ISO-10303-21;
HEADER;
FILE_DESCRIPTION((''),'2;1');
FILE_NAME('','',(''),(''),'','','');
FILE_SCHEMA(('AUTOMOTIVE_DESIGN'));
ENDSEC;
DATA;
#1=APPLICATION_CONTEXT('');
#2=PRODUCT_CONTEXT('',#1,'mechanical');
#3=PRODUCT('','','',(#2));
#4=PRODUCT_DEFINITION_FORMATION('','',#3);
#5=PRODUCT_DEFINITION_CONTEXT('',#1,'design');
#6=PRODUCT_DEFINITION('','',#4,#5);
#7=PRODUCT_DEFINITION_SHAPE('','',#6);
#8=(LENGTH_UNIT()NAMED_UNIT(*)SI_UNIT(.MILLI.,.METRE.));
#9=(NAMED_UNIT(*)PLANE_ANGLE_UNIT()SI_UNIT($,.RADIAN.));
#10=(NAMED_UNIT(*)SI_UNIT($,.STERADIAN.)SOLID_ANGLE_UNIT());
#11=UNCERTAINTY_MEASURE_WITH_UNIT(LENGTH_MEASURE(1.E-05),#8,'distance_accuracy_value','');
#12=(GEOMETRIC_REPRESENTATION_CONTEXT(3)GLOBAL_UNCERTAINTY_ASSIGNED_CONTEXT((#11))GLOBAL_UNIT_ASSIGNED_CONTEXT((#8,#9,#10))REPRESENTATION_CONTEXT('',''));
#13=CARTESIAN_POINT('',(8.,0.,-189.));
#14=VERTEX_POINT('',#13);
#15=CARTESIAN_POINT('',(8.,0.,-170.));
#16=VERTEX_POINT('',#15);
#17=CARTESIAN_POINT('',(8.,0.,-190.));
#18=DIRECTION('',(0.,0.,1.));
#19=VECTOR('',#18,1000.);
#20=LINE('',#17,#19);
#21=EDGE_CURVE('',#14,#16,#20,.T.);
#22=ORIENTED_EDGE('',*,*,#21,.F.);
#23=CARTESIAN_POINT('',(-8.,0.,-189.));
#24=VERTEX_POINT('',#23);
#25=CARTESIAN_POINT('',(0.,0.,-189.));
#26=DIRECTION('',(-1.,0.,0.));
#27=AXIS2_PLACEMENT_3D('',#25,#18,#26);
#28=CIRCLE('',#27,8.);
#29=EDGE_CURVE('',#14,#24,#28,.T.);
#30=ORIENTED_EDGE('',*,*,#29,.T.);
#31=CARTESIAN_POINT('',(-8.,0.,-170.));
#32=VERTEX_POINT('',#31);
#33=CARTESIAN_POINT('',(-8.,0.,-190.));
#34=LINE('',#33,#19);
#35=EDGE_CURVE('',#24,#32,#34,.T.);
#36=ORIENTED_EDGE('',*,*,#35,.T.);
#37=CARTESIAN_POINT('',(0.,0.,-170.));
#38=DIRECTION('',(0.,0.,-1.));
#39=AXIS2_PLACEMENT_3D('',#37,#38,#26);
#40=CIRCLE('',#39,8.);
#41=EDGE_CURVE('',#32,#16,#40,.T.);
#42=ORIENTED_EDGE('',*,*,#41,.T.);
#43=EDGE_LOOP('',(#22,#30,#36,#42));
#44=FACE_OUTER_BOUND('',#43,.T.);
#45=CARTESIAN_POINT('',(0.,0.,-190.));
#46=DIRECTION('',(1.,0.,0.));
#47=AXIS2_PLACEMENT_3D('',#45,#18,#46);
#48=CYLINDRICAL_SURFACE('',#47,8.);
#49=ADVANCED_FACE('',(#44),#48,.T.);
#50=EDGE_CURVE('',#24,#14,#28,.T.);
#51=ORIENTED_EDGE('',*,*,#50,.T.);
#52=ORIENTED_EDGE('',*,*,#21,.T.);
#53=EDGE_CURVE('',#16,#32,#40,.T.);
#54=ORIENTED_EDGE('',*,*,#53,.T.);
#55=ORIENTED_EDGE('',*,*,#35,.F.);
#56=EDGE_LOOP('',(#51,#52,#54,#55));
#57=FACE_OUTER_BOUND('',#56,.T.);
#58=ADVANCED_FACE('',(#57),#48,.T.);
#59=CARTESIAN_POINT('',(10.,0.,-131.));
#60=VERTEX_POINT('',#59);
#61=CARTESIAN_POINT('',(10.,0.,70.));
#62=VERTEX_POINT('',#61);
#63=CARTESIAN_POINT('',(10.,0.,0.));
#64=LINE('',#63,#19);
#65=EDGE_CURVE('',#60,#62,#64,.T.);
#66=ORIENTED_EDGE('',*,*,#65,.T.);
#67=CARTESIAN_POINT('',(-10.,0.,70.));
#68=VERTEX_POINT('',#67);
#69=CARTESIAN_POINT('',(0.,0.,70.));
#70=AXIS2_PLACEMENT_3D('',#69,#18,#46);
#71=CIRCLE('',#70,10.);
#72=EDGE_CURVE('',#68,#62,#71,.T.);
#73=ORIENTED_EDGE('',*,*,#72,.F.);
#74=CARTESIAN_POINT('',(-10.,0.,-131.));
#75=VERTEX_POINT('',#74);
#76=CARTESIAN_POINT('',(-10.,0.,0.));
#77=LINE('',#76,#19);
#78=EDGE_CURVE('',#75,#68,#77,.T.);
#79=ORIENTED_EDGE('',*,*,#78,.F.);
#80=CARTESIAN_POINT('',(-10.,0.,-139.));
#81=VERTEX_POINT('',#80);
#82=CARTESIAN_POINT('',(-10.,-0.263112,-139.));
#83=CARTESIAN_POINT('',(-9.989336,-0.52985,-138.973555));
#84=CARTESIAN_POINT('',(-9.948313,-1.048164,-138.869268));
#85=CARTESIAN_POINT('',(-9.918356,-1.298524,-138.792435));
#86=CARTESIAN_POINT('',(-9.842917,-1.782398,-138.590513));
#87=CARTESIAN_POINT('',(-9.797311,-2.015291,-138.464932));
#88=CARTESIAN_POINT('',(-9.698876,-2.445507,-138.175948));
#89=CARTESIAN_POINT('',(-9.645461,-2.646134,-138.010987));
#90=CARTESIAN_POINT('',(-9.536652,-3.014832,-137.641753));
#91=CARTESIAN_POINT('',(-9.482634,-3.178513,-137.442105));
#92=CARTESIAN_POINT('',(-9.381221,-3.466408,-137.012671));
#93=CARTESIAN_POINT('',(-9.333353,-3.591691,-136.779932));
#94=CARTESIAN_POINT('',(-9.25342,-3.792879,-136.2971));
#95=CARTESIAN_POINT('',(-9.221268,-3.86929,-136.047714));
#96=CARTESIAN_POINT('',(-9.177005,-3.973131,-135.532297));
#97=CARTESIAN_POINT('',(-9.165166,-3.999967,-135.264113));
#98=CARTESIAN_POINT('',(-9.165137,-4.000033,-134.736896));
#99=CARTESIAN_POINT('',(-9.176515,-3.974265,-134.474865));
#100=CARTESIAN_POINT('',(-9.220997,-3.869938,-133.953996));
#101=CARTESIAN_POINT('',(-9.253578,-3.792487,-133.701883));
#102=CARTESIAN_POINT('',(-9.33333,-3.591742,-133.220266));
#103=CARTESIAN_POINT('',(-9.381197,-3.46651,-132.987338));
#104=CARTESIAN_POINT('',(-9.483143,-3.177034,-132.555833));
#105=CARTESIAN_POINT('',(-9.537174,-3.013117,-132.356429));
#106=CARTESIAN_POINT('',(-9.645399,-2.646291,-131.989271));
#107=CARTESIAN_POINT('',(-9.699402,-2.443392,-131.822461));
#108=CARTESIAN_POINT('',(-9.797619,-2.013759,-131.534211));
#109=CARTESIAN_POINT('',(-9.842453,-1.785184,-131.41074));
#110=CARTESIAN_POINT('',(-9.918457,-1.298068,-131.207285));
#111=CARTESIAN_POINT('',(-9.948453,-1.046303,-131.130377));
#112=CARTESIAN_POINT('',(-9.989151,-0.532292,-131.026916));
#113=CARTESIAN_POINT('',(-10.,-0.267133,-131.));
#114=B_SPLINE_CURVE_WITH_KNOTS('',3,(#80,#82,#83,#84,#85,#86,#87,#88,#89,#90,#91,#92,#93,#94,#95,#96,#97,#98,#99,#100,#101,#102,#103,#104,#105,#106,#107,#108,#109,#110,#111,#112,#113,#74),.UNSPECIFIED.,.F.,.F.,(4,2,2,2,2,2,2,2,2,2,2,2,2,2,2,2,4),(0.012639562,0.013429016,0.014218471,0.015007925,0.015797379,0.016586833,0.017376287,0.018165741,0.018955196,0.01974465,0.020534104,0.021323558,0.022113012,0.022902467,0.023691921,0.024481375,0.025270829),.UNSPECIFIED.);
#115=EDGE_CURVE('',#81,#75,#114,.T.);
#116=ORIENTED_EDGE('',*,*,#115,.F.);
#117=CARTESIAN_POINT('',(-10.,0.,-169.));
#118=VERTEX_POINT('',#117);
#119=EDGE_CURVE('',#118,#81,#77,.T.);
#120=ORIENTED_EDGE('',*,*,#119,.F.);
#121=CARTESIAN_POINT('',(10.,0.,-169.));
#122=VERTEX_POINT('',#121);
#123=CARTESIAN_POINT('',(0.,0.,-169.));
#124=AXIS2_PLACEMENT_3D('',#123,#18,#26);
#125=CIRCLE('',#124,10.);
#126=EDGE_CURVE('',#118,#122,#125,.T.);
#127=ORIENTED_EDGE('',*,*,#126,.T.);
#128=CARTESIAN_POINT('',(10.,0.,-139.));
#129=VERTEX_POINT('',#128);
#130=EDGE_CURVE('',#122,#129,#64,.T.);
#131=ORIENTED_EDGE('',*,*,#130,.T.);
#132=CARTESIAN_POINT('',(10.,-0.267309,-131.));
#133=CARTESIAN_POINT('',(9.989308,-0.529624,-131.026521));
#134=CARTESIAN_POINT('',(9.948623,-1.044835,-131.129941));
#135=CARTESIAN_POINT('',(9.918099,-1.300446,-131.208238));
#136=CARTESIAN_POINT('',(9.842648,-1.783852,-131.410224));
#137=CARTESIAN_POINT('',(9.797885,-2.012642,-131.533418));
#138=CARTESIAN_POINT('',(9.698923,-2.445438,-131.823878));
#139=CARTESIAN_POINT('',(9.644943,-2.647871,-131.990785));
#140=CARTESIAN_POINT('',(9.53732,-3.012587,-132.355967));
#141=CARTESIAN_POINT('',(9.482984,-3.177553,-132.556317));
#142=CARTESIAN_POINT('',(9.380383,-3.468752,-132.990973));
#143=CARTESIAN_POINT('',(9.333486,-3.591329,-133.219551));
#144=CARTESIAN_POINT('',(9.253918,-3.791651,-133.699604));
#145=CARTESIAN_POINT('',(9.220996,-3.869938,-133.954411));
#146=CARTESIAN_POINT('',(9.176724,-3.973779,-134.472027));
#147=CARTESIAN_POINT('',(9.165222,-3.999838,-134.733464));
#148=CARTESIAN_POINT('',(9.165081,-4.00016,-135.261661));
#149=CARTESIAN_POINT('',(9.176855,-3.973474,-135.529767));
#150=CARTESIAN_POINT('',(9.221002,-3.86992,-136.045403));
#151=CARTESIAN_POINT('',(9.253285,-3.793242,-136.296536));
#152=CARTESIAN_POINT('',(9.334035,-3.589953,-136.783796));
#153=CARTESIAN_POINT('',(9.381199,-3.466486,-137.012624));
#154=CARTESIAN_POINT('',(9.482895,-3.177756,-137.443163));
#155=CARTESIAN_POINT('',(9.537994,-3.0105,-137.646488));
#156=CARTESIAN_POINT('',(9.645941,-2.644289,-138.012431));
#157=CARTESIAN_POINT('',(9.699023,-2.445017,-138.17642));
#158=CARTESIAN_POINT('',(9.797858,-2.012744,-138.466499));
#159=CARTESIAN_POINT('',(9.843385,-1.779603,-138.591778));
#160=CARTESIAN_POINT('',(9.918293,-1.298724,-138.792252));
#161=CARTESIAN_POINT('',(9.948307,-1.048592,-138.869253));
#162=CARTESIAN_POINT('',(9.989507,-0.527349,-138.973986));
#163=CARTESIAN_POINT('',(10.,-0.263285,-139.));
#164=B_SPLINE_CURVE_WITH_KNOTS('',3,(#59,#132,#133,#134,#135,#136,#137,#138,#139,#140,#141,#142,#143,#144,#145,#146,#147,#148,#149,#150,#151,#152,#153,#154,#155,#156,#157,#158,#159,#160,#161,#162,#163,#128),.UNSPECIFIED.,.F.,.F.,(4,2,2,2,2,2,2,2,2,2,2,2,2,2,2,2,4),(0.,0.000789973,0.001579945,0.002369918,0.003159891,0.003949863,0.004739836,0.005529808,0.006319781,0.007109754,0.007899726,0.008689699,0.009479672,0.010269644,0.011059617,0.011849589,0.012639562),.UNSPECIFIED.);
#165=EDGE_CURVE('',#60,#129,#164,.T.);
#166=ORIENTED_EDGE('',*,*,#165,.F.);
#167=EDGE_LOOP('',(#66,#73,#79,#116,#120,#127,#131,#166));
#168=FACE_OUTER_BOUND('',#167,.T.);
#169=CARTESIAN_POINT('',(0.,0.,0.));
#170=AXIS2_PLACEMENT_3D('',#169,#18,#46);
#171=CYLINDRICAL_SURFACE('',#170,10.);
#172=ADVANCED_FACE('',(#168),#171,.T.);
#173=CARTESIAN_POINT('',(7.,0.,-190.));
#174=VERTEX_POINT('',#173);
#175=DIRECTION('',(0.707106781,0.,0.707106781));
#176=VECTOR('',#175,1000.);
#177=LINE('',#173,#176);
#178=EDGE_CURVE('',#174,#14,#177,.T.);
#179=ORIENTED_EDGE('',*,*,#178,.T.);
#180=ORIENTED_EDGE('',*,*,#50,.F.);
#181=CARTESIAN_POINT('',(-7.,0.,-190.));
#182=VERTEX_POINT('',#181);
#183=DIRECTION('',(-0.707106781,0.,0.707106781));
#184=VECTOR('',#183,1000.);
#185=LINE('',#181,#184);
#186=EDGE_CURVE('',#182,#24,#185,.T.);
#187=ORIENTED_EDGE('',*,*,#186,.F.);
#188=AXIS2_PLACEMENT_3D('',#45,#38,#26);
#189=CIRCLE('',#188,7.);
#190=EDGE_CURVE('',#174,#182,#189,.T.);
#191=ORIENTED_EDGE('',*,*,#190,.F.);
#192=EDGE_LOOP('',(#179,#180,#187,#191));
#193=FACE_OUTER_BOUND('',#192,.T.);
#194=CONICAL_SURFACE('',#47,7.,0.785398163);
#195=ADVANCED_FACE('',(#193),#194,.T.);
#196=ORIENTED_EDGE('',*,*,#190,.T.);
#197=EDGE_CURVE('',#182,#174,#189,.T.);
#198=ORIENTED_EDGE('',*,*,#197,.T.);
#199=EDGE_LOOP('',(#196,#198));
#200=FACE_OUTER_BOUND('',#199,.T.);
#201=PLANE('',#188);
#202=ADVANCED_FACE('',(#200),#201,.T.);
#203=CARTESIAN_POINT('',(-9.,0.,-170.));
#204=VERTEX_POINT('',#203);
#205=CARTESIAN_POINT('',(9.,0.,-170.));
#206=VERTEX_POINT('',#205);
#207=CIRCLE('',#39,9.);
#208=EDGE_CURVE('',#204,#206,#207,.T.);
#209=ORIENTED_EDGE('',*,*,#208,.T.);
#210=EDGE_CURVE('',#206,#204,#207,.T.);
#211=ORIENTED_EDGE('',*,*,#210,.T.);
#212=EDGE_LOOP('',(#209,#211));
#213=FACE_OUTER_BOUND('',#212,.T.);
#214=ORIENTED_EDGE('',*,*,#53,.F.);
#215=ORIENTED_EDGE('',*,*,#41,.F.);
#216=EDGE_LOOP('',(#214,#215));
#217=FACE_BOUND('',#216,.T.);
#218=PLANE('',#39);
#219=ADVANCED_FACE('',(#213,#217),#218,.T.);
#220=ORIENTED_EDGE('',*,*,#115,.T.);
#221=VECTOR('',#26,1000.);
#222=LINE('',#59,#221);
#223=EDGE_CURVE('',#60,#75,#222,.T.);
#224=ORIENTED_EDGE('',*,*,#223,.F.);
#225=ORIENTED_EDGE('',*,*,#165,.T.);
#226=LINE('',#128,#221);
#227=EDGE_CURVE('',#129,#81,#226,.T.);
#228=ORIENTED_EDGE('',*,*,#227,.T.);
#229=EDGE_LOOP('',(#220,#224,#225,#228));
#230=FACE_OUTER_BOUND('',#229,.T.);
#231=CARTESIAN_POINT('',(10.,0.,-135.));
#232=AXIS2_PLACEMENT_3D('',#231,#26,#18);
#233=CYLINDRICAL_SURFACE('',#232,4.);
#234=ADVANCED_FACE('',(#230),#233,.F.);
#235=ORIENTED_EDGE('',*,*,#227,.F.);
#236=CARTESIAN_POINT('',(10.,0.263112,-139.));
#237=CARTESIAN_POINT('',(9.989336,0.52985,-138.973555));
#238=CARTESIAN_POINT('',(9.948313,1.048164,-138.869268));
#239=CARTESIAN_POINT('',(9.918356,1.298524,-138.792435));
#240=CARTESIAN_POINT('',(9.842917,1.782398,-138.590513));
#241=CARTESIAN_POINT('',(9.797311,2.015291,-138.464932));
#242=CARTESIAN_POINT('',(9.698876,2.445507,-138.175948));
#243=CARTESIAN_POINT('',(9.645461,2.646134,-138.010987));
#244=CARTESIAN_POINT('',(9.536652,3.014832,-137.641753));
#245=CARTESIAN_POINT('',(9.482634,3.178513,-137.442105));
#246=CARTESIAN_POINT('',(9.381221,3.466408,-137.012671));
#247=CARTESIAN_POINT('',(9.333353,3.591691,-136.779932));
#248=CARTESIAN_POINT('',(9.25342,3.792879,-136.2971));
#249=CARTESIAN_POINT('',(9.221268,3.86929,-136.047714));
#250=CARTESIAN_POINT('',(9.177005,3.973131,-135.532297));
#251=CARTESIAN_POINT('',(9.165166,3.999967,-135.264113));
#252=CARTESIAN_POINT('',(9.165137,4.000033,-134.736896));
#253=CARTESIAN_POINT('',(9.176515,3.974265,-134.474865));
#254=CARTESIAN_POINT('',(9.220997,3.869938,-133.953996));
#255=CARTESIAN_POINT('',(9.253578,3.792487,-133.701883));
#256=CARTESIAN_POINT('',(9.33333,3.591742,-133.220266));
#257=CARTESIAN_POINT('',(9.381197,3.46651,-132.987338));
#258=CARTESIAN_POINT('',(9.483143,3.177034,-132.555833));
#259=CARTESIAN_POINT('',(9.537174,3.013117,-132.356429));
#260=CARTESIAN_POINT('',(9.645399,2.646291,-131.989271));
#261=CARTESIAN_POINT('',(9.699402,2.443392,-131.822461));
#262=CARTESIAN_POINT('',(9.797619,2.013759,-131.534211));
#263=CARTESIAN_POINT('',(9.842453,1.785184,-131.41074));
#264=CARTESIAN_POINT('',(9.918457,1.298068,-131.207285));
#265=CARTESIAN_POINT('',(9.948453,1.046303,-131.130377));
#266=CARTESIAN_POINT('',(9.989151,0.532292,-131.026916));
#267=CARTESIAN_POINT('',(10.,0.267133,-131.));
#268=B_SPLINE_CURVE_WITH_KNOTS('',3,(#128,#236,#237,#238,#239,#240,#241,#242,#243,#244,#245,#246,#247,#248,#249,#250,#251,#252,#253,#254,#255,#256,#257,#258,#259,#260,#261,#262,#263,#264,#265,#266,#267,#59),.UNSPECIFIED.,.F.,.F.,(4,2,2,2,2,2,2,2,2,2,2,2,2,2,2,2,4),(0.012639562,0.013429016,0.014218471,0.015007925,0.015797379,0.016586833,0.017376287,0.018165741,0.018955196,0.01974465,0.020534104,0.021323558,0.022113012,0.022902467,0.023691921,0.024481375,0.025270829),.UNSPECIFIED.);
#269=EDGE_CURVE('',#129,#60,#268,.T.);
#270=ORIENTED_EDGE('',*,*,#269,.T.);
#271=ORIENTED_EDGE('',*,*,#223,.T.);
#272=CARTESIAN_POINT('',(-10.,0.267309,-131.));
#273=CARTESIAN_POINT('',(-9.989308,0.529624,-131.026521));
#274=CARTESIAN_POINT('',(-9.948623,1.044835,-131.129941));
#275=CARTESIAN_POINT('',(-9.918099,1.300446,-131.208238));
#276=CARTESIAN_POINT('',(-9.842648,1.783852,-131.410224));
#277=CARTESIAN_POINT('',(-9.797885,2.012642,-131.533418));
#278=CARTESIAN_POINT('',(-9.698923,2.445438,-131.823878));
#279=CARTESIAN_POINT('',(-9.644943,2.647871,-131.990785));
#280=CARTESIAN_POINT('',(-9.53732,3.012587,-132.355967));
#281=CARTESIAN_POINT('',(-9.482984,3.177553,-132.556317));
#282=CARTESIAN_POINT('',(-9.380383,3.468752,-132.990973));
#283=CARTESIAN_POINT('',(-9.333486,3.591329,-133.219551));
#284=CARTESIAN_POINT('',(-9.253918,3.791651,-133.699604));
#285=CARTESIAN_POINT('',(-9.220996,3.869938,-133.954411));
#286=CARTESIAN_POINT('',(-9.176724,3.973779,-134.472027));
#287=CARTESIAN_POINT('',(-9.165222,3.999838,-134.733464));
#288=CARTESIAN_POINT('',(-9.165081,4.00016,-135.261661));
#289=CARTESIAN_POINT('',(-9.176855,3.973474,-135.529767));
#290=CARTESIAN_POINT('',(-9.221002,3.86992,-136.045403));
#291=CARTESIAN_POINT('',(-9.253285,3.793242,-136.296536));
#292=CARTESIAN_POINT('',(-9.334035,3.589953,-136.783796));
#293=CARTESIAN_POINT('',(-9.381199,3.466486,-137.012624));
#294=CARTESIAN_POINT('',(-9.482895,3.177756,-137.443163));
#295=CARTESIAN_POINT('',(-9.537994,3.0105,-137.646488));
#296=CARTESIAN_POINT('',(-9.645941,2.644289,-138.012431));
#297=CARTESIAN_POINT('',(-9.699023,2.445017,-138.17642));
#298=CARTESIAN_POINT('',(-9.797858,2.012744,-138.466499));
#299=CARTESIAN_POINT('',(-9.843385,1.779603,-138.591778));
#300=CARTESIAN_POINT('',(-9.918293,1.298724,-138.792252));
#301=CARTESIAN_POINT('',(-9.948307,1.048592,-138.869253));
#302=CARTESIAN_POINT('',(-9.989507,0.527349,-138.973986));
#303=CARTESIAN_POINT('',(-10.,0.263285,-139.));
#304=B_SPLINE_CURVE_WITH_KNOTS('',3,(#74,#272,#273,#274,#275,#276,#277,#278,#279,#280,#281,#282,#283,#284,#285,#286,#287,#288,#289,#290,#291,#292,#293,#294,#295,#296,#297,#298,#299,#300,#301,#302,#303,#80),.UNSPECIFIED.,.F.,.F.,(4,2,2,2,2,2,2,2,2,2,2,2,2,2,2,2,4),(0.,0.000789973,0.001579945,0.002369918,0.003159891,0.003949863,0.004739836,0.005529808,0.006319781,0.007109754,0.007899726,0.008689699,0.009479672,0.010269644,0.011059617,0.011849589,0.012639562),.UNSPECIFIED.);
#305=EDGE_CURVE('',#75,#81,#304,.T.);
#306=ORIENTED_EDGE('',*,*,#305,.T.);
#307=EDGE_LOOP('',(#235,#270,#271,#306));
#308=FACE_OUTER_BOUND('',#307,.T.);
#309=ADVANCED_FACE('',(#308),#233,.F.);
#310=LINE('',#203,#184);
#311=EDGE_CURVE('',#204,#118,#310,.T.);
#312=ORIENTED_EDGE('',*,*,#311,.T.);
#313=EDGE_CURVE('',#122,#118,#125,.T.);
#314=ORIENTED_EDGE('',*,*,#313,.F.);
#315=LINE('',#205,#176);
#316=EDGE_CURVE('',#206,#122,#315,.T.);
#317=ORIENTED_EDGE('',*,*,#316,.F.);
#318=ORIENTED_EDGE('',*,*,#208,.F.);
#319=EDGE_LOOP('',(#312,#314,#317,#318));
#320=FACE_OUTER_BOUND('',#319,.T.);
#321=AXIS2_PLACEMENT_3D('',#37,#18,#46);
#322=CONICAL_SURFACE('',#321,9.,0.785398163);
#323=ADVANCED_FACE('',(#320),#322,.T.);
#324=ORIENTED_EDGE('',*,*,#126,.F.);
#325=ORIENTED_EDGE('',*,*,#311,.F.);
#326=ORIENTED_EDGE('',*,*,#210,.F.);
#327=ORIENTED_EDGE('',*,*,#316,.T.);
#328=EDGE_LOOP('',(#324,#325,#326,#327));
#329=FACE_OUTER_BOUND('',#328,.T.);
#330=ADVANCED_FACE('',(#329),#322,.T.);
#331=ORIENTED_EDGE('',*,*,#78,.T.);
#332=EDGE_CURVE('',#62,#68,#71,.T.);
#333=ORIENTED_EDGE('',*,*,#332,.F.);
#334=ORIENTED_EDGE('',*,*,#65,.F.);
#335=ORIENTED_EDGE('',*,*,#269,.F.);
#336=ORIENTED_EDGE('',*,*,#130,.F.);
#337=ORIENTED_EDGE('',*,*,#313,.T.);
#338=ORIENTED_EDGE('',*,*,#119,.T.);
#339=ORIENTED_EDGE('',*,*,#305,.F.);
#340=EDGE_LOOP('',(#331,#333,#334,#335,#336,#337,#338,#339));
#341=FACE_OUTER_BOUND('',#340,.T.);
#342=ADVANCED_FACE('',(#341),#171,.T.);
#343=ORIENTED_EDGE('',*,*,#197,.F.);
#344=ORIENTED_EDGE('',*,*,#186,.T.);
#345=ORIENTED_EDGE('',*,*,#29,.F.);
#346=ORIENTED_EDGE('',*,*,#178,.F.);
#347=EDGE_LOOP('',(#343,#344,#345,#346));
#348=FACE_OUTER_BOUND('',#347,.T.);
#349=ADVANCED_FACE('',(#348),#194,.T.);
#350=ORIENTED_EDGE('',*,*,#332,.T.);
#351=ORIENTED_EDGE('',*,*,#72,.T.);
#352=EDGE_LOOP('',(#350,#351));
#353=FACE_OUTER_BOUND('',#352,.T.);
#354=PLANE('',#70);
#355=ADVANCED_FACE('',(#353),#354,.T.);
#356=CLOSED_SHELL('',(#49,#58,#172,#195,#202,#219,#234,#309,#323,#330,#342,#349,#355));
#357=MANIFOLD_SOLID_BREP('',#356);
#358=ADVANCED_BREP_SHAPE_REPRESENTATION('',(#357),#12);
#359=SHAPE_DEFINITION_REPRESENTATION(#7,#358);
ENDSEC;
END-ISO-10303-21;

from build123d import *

# Parameters (mm, degrees)
SKETCH2_W               = 150
SKETCH2_H               = 10
CUT_EXTRUDE1_DEPTH      = 10
CUT_EXTRUDE1_DEPTH_BACK = 10
SKETCH5_R               = 4
BOSS_EXTRUDE3_START     = 70
SKETCH7_R               = 10
BOSS_EXTRUDE3_DEPTH     = 70
SKETCH3_R               = 10
BOSS_EXTRUDE4_DEPTH     = 20
SKETCH8_R               = 8
BOSS_EXTRUDE5_DEPTH     = 20
CHAMFER1_SIZE           = 1
CHAMFER2_SIZE           = 1


with BuildPart() as part:
    # Sketch2 → Revolve4 (revolve)
    with BuildSketch(Plane(origin=(0, 0, 0), x_dir=(0, 0, -1), z_dir=(1, 0, 0)), mode=Mode.PRIVATE) as revolve4_sk:
        with Locations((75, 5)):
            Rectangle(SKETCH2_W, SKETCH2_H)
    revolve(revolve4_sk.sketch.rotate(Axis((0, 0, 0), (0, 0, -1)), 90), axis=Axis((0, 0, 0), (0, 0, -1)))

    # Sketch5 → Cut-Extrude1 (cut, two sides: drawn at the far end of the back side and taken through both)
    with BuildSketch(Plane(origin=(0, 0, 0), x_dir=(0, 0, -1), z_dir=(1, 0, 0)).offset(-CUT_EXTRUDE1_DEPTH_BACK)):
        with Locations(Location((135, 0, 0), (0, 0, 180))):
            Circle(SKETCH5_R)
    extrude(amount=CUT_EXTRUDE1_DEPTH + CUT_EXTRUDE1_DEPTH_BACK, mode=Mode.SUBTRACT)

    # Sketch7 → Boss-Extrude3 (add)
    with BuildSketch(Plane.XY.offset(BOSS_EXTRUDE3_START)):
        Circle(SKETCH7_R)
    extrude(amount=-BOSS_EXTRUDE3_DEPTH)

    # Sketch3 → Boss-Extrude4 (add)
    with BuildSketch(Plane(origin=(0, 0, -150), x_dir=(-1, 0, 0), z_dir=(0, 0, -1))):
        with Locations(Location((0, 0, 0), (0, 0, 180))):
            Circle(SKETCH3_R)
    extrude(amount=BOSS_EXTRUDE4_DEPTH)

    # Sketch8 → Boss-Extrude5 (add)
    with BuildSketch(Plane(origin=(0, 0, -170), x_dir=(-1, 0, 0), z_dir=(0, 0, -1))):
        Circle(SKETCH8_R)
    extrude(amount=BOSS_EXTRUDE5_DEPTH)

    # Chamfer1
    chamfer1_edges = [part.edges().sort_by_distance(p)[0] for p in [
        (8, 0, -190),
    ]]
    chamfer(chamfer1_edges, length=CHAMFER1_SIZE)

    # Chamfer2
    chamfer2_edges = [part.edges().sort_by_distance(p)[0] for p in [
        (-10, 0, -170),
    ]]
    chamfer(chamfer2_edges, length=CHAMFER2_SIZE)


solid = part.part
